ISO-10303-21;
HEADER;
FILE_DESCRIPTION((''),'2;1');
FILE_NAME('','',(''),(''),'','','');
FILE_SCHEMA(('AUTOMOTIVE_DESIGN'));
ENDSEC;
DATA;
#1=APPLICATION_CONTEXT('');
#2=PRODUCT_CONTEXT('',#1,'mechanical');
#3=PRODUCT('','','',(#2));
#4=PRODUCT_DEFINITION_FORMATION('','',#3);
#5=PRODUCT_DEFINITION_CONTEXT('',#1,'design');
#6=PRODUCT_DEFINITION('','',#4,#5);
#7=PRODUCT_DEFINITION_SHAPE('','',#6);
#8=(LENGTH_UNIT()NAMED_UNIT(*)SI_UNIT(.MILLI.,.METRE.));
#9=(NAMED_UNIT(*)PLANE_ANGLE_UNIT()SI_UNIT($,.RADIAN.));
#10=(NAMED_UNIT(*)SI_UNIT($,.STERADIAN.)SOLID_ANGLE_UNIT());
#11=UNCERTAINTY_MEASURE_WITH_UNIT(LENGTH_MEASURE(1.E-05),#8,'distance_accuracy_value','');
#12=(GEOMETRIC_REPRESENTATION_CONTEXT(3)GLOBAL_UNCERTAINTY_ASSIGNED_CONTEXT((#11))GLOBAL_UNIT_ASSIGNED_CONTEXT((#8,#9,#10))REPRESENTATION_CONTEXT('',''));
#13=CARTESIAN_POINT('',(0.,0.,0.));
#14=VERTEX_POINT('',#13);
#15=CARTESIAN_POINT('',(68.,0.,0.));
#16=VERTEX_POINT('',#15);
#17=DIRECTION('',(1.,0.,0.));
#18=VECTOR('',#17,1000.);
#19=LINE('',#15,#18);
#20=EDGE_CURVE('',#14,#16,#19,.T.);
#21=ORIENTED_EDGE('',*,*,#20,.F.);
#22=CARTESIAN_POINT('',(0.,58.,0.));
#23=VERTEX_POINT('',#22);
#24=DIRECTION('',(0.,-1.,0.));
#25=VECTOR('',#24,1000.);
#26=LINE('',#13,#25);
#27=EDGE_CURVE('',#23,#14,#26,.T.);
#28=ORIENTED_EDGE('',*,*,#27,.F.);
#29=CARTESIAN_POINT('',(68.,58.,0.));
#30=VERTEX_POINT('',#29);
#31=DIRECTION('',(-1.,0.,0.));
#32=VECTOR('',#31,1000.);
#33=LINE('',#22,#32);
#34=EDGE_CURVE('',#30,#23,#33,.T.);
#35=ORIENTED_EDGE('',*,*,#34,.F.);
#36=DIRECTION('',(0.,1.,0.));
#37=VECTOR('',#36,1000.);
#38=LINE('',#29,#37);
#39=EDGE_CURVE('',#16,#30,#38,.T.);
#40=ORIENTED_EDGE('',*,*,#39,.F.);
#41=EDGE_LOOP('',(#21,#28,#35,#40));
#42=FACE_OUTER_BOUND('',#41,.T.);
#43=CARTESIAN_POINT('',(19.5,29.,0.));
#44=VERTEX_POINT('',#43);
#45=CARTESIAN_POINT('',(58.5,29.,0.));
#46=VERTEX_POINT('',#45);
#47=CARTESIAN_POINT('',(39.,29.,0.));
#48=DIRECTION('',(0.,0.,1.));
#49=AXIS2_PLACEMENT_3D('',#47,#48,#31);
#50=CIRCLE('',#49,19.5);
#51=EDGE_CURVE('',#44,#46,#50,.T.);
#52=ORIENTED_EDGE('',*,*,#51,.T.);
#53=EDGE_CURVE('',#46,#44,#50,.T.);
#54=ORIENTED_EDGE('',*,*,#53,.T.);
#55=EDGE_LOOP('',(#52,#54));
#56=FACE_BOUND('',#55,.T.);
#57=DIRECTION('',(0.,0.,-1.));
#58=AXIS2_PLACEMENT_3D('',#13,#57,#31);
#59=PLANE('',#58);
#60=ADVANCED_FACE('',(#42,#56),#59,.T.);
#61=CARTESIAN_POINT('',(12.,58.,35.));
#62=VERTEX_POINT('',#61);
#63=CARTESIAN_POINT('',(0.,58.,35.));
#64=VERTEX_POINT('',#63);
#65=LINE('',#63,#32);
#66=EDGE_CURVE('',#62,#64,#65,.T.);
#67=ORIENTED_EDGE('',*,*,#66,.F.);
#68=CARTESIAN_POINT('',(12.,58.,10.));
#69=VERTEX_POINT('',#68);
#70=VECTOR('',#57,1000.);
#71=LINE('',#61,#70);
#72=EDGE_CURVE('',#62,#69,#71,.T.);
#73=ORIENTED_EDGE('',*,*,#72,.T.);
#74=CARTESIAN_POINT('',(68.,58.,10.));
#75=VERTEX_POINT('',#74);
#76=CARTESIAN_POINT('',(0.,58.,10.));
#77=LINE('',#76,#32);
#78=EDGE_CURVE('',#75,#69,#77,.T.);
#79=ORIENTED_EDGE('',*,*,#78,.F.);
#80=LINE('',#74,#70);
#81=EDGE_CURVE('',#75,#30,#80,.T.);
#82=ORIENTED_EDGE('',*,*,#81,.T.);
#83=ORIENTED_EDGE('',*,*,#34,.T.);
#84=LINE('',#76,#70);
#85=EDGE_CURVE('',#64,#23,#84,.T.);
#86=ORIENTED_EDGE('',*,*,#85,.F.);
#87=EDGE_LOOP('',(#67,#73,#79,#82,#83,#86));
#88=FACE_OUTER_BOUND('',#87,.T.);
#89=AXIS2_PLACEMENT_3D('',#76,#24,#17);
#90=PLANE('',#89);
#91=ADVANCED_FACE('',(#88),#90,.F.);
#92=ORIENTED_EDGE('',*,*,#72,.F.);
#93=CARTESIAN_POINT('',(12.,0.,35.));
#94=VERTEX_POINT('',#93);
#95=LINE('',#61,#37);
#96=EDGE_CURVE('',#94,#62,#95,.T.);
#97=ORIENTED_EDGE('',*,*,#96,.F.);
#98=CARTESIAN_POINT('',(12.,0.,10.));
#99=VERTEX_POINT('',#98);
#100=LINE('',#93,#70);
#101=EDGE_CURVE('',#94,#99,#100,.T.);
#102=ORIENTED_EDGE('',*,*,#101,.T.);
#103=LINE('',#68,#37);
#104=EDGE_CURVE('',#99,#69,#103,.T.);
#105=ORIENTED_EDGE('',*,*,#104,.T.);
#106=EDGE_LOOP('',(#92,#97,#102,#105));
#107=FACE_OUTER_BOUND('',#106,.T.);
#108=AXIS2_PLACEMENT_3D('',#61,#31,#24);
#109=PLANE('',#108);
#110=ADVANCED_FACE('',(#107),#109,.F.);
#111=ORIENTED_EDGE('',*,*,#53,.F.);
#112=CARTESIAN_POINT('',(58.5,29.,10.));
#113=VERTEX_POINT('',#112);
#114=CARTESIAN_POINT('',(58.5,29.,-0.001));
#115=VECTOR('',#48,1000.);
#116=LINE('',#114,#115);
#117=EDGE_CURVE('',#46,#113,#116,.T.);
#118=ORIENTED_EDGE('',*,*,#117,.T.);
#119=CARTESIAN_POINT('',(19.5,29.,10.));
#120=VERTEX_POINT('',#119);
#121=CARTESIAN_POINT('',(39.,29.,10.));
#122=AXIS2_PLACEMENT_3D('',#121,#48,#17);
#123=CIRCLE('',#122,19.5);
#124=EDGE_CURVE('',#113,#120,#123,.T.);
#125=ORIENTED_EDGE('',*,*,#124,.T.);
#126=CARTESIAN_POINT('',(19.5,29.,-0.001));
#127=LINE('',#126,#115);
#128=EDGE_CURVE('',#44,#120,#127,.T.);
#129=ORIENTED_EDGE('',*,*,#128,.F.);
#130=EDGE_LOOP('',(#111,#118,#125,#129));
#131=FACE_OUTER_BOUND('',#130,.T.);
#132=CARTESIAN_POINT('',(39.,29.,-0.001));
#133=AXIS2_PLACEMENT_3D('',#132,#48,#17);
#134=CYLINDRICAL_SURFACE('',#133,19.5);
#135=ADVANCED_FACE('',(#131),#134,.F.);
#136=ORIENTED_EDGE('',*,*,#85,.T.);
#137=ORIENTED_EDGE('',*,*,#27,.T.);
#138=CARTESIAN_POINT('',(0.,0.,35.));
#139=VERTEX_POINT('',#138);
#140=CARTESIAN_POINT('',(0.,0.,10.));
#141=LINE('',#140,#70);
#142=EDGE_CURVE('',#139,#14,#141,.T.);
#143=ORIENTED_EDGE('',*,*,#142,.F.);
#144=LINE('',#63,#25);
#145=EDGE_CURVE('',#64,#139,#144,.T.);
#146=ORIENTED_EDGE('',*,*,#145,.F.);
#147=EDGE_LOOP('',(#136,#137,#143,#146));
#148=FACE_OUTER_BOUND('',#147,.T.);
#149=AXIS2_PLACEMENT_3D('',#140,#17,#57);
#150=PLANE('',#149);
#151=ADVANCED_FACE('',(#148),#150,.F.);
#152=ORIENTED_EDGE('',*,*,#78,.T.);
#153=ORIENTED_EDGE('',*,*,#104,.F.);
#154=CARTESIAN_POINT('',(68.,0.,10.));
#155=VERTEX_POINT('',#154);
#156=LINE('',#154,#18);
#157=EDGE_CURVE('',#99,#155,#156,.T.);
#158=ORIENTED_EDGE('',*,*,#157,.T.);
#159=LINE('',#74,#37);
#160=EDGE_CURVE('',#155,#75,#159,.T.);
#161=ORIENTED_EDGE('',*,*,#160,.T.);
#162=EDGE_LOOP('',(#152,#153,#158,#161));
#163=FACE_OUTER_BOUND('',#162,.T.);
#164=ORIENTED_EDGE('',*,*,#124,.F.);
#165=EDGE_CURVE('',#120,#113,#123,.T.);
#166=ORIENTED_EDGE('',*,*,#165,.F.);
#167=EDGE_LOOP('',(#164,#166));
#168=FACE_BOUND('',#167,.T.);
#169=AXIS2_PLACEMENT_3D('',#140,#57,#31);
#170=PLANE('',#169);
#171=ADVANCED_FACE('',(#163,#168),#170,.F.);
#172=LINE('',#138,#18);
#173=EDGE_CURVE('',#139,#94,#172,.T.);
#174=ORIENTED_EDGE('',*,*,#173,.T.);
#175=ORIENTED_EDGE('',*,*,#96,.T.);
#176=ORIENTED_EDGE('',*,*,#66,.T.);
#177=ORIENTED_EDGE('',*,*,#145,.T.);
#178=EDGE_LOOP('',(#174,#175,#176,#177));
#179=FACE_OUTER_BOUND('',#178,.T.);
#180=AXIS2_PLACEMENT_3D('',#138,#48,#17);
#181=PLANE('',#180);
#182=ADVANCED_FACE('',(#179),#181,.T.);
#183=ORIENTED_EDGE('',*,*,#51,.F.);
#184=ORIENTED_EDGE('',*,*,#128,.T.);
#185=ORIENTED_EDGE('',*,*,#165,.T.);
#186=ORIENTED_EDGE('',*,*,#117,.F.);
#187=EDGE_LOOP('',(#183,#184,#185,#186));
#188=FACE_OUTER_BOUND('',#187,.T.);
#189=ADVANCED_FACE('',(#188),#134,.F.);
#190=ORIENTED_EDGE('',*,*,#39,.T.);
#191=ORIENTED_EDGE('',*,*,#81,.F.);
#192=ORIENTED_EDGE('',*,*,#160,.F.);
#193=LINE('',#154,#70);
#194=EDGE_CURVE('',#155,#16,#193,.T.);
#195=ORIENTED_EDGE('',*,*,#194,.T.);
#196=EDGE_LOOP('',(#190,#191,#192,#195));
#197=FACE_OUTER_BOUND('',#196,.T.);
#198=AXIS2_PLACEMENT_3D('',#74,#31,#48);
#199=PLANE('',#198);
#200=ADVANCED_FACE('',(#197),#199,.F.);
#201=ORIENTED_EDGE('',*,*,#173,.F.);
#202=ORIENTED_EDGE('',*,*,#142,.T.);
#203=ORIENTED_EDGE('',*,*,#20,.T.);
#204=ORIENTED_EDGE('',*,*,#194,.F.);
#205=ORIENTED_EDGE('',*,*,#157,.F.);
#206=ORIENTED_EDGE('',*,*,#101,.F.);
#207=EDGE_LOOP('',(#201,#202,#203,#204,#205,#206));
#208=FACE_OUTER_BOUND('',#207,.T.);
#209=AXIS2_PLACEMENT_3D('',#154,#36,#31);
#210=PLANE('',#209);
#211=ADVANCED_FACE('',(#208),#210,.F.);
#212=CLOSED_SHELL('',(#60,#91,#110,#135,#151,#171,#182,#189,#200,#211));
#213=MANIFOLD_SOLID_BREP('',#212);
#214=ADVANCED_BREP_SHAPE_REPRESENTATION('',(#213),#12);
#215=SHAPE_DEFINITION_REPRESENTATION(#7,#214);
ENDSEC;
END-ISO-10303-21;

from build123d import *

# Parameters (mm, degrees)
SKETCH_1_W          = 68
SKETCH_1_H          = 58
EXTRUDE_1_DEPTH     = 10
CUT_EXTRUDE_1_REACH = 91.933
SKETCH_2_R          = 19.5
SKETCH_4_W          = 12
SKETCH_4_H          = 58
EXTRUDE_3_DEPTH     = 25


with BuildPart() as part:
    # 草图1 → 凸台-拉伸1 (new body)
    with BuildSketch(Plane.XY):
        with Locations((34, 29)):
            Rectangle(SKETCH_1_W, SKETCH_1_H)
    extrude(amount=EXTRUDE_1_DEPTH)

    # 草图2 → 切除-拉伸1 (cut, up to next)
    with BuildSketch(Plane.XY.offset(10), mode=Mode.PRIVATE) as cut_extrude_1_sk1:
        with Locations((39, 29)):
            Circle(SKETCH_2_R)
    cut_extrude_1_tool1 = extrude(cut_extrude_1_sk1.sketch, amount=-CUT_EXTRUDE_1_REACH, mode=Mode.PRIVATE) & part.part
    add(cut_extrude_1_tool1.solids().sort_by_distance((39, 29, 10))[0], mode=Mode.SUBTRACT)

    # 草图4 → 凸台-拉伸3 (add)
    with BuildSketch(Plane.XY.offset(10)):
        with Locations((6, 29)):
            Rectangle(SKETCH_4_W, SKETCH_4_H)
    extrude(amount=EXTRUDE_3_DEPTH)


solid = part.part
